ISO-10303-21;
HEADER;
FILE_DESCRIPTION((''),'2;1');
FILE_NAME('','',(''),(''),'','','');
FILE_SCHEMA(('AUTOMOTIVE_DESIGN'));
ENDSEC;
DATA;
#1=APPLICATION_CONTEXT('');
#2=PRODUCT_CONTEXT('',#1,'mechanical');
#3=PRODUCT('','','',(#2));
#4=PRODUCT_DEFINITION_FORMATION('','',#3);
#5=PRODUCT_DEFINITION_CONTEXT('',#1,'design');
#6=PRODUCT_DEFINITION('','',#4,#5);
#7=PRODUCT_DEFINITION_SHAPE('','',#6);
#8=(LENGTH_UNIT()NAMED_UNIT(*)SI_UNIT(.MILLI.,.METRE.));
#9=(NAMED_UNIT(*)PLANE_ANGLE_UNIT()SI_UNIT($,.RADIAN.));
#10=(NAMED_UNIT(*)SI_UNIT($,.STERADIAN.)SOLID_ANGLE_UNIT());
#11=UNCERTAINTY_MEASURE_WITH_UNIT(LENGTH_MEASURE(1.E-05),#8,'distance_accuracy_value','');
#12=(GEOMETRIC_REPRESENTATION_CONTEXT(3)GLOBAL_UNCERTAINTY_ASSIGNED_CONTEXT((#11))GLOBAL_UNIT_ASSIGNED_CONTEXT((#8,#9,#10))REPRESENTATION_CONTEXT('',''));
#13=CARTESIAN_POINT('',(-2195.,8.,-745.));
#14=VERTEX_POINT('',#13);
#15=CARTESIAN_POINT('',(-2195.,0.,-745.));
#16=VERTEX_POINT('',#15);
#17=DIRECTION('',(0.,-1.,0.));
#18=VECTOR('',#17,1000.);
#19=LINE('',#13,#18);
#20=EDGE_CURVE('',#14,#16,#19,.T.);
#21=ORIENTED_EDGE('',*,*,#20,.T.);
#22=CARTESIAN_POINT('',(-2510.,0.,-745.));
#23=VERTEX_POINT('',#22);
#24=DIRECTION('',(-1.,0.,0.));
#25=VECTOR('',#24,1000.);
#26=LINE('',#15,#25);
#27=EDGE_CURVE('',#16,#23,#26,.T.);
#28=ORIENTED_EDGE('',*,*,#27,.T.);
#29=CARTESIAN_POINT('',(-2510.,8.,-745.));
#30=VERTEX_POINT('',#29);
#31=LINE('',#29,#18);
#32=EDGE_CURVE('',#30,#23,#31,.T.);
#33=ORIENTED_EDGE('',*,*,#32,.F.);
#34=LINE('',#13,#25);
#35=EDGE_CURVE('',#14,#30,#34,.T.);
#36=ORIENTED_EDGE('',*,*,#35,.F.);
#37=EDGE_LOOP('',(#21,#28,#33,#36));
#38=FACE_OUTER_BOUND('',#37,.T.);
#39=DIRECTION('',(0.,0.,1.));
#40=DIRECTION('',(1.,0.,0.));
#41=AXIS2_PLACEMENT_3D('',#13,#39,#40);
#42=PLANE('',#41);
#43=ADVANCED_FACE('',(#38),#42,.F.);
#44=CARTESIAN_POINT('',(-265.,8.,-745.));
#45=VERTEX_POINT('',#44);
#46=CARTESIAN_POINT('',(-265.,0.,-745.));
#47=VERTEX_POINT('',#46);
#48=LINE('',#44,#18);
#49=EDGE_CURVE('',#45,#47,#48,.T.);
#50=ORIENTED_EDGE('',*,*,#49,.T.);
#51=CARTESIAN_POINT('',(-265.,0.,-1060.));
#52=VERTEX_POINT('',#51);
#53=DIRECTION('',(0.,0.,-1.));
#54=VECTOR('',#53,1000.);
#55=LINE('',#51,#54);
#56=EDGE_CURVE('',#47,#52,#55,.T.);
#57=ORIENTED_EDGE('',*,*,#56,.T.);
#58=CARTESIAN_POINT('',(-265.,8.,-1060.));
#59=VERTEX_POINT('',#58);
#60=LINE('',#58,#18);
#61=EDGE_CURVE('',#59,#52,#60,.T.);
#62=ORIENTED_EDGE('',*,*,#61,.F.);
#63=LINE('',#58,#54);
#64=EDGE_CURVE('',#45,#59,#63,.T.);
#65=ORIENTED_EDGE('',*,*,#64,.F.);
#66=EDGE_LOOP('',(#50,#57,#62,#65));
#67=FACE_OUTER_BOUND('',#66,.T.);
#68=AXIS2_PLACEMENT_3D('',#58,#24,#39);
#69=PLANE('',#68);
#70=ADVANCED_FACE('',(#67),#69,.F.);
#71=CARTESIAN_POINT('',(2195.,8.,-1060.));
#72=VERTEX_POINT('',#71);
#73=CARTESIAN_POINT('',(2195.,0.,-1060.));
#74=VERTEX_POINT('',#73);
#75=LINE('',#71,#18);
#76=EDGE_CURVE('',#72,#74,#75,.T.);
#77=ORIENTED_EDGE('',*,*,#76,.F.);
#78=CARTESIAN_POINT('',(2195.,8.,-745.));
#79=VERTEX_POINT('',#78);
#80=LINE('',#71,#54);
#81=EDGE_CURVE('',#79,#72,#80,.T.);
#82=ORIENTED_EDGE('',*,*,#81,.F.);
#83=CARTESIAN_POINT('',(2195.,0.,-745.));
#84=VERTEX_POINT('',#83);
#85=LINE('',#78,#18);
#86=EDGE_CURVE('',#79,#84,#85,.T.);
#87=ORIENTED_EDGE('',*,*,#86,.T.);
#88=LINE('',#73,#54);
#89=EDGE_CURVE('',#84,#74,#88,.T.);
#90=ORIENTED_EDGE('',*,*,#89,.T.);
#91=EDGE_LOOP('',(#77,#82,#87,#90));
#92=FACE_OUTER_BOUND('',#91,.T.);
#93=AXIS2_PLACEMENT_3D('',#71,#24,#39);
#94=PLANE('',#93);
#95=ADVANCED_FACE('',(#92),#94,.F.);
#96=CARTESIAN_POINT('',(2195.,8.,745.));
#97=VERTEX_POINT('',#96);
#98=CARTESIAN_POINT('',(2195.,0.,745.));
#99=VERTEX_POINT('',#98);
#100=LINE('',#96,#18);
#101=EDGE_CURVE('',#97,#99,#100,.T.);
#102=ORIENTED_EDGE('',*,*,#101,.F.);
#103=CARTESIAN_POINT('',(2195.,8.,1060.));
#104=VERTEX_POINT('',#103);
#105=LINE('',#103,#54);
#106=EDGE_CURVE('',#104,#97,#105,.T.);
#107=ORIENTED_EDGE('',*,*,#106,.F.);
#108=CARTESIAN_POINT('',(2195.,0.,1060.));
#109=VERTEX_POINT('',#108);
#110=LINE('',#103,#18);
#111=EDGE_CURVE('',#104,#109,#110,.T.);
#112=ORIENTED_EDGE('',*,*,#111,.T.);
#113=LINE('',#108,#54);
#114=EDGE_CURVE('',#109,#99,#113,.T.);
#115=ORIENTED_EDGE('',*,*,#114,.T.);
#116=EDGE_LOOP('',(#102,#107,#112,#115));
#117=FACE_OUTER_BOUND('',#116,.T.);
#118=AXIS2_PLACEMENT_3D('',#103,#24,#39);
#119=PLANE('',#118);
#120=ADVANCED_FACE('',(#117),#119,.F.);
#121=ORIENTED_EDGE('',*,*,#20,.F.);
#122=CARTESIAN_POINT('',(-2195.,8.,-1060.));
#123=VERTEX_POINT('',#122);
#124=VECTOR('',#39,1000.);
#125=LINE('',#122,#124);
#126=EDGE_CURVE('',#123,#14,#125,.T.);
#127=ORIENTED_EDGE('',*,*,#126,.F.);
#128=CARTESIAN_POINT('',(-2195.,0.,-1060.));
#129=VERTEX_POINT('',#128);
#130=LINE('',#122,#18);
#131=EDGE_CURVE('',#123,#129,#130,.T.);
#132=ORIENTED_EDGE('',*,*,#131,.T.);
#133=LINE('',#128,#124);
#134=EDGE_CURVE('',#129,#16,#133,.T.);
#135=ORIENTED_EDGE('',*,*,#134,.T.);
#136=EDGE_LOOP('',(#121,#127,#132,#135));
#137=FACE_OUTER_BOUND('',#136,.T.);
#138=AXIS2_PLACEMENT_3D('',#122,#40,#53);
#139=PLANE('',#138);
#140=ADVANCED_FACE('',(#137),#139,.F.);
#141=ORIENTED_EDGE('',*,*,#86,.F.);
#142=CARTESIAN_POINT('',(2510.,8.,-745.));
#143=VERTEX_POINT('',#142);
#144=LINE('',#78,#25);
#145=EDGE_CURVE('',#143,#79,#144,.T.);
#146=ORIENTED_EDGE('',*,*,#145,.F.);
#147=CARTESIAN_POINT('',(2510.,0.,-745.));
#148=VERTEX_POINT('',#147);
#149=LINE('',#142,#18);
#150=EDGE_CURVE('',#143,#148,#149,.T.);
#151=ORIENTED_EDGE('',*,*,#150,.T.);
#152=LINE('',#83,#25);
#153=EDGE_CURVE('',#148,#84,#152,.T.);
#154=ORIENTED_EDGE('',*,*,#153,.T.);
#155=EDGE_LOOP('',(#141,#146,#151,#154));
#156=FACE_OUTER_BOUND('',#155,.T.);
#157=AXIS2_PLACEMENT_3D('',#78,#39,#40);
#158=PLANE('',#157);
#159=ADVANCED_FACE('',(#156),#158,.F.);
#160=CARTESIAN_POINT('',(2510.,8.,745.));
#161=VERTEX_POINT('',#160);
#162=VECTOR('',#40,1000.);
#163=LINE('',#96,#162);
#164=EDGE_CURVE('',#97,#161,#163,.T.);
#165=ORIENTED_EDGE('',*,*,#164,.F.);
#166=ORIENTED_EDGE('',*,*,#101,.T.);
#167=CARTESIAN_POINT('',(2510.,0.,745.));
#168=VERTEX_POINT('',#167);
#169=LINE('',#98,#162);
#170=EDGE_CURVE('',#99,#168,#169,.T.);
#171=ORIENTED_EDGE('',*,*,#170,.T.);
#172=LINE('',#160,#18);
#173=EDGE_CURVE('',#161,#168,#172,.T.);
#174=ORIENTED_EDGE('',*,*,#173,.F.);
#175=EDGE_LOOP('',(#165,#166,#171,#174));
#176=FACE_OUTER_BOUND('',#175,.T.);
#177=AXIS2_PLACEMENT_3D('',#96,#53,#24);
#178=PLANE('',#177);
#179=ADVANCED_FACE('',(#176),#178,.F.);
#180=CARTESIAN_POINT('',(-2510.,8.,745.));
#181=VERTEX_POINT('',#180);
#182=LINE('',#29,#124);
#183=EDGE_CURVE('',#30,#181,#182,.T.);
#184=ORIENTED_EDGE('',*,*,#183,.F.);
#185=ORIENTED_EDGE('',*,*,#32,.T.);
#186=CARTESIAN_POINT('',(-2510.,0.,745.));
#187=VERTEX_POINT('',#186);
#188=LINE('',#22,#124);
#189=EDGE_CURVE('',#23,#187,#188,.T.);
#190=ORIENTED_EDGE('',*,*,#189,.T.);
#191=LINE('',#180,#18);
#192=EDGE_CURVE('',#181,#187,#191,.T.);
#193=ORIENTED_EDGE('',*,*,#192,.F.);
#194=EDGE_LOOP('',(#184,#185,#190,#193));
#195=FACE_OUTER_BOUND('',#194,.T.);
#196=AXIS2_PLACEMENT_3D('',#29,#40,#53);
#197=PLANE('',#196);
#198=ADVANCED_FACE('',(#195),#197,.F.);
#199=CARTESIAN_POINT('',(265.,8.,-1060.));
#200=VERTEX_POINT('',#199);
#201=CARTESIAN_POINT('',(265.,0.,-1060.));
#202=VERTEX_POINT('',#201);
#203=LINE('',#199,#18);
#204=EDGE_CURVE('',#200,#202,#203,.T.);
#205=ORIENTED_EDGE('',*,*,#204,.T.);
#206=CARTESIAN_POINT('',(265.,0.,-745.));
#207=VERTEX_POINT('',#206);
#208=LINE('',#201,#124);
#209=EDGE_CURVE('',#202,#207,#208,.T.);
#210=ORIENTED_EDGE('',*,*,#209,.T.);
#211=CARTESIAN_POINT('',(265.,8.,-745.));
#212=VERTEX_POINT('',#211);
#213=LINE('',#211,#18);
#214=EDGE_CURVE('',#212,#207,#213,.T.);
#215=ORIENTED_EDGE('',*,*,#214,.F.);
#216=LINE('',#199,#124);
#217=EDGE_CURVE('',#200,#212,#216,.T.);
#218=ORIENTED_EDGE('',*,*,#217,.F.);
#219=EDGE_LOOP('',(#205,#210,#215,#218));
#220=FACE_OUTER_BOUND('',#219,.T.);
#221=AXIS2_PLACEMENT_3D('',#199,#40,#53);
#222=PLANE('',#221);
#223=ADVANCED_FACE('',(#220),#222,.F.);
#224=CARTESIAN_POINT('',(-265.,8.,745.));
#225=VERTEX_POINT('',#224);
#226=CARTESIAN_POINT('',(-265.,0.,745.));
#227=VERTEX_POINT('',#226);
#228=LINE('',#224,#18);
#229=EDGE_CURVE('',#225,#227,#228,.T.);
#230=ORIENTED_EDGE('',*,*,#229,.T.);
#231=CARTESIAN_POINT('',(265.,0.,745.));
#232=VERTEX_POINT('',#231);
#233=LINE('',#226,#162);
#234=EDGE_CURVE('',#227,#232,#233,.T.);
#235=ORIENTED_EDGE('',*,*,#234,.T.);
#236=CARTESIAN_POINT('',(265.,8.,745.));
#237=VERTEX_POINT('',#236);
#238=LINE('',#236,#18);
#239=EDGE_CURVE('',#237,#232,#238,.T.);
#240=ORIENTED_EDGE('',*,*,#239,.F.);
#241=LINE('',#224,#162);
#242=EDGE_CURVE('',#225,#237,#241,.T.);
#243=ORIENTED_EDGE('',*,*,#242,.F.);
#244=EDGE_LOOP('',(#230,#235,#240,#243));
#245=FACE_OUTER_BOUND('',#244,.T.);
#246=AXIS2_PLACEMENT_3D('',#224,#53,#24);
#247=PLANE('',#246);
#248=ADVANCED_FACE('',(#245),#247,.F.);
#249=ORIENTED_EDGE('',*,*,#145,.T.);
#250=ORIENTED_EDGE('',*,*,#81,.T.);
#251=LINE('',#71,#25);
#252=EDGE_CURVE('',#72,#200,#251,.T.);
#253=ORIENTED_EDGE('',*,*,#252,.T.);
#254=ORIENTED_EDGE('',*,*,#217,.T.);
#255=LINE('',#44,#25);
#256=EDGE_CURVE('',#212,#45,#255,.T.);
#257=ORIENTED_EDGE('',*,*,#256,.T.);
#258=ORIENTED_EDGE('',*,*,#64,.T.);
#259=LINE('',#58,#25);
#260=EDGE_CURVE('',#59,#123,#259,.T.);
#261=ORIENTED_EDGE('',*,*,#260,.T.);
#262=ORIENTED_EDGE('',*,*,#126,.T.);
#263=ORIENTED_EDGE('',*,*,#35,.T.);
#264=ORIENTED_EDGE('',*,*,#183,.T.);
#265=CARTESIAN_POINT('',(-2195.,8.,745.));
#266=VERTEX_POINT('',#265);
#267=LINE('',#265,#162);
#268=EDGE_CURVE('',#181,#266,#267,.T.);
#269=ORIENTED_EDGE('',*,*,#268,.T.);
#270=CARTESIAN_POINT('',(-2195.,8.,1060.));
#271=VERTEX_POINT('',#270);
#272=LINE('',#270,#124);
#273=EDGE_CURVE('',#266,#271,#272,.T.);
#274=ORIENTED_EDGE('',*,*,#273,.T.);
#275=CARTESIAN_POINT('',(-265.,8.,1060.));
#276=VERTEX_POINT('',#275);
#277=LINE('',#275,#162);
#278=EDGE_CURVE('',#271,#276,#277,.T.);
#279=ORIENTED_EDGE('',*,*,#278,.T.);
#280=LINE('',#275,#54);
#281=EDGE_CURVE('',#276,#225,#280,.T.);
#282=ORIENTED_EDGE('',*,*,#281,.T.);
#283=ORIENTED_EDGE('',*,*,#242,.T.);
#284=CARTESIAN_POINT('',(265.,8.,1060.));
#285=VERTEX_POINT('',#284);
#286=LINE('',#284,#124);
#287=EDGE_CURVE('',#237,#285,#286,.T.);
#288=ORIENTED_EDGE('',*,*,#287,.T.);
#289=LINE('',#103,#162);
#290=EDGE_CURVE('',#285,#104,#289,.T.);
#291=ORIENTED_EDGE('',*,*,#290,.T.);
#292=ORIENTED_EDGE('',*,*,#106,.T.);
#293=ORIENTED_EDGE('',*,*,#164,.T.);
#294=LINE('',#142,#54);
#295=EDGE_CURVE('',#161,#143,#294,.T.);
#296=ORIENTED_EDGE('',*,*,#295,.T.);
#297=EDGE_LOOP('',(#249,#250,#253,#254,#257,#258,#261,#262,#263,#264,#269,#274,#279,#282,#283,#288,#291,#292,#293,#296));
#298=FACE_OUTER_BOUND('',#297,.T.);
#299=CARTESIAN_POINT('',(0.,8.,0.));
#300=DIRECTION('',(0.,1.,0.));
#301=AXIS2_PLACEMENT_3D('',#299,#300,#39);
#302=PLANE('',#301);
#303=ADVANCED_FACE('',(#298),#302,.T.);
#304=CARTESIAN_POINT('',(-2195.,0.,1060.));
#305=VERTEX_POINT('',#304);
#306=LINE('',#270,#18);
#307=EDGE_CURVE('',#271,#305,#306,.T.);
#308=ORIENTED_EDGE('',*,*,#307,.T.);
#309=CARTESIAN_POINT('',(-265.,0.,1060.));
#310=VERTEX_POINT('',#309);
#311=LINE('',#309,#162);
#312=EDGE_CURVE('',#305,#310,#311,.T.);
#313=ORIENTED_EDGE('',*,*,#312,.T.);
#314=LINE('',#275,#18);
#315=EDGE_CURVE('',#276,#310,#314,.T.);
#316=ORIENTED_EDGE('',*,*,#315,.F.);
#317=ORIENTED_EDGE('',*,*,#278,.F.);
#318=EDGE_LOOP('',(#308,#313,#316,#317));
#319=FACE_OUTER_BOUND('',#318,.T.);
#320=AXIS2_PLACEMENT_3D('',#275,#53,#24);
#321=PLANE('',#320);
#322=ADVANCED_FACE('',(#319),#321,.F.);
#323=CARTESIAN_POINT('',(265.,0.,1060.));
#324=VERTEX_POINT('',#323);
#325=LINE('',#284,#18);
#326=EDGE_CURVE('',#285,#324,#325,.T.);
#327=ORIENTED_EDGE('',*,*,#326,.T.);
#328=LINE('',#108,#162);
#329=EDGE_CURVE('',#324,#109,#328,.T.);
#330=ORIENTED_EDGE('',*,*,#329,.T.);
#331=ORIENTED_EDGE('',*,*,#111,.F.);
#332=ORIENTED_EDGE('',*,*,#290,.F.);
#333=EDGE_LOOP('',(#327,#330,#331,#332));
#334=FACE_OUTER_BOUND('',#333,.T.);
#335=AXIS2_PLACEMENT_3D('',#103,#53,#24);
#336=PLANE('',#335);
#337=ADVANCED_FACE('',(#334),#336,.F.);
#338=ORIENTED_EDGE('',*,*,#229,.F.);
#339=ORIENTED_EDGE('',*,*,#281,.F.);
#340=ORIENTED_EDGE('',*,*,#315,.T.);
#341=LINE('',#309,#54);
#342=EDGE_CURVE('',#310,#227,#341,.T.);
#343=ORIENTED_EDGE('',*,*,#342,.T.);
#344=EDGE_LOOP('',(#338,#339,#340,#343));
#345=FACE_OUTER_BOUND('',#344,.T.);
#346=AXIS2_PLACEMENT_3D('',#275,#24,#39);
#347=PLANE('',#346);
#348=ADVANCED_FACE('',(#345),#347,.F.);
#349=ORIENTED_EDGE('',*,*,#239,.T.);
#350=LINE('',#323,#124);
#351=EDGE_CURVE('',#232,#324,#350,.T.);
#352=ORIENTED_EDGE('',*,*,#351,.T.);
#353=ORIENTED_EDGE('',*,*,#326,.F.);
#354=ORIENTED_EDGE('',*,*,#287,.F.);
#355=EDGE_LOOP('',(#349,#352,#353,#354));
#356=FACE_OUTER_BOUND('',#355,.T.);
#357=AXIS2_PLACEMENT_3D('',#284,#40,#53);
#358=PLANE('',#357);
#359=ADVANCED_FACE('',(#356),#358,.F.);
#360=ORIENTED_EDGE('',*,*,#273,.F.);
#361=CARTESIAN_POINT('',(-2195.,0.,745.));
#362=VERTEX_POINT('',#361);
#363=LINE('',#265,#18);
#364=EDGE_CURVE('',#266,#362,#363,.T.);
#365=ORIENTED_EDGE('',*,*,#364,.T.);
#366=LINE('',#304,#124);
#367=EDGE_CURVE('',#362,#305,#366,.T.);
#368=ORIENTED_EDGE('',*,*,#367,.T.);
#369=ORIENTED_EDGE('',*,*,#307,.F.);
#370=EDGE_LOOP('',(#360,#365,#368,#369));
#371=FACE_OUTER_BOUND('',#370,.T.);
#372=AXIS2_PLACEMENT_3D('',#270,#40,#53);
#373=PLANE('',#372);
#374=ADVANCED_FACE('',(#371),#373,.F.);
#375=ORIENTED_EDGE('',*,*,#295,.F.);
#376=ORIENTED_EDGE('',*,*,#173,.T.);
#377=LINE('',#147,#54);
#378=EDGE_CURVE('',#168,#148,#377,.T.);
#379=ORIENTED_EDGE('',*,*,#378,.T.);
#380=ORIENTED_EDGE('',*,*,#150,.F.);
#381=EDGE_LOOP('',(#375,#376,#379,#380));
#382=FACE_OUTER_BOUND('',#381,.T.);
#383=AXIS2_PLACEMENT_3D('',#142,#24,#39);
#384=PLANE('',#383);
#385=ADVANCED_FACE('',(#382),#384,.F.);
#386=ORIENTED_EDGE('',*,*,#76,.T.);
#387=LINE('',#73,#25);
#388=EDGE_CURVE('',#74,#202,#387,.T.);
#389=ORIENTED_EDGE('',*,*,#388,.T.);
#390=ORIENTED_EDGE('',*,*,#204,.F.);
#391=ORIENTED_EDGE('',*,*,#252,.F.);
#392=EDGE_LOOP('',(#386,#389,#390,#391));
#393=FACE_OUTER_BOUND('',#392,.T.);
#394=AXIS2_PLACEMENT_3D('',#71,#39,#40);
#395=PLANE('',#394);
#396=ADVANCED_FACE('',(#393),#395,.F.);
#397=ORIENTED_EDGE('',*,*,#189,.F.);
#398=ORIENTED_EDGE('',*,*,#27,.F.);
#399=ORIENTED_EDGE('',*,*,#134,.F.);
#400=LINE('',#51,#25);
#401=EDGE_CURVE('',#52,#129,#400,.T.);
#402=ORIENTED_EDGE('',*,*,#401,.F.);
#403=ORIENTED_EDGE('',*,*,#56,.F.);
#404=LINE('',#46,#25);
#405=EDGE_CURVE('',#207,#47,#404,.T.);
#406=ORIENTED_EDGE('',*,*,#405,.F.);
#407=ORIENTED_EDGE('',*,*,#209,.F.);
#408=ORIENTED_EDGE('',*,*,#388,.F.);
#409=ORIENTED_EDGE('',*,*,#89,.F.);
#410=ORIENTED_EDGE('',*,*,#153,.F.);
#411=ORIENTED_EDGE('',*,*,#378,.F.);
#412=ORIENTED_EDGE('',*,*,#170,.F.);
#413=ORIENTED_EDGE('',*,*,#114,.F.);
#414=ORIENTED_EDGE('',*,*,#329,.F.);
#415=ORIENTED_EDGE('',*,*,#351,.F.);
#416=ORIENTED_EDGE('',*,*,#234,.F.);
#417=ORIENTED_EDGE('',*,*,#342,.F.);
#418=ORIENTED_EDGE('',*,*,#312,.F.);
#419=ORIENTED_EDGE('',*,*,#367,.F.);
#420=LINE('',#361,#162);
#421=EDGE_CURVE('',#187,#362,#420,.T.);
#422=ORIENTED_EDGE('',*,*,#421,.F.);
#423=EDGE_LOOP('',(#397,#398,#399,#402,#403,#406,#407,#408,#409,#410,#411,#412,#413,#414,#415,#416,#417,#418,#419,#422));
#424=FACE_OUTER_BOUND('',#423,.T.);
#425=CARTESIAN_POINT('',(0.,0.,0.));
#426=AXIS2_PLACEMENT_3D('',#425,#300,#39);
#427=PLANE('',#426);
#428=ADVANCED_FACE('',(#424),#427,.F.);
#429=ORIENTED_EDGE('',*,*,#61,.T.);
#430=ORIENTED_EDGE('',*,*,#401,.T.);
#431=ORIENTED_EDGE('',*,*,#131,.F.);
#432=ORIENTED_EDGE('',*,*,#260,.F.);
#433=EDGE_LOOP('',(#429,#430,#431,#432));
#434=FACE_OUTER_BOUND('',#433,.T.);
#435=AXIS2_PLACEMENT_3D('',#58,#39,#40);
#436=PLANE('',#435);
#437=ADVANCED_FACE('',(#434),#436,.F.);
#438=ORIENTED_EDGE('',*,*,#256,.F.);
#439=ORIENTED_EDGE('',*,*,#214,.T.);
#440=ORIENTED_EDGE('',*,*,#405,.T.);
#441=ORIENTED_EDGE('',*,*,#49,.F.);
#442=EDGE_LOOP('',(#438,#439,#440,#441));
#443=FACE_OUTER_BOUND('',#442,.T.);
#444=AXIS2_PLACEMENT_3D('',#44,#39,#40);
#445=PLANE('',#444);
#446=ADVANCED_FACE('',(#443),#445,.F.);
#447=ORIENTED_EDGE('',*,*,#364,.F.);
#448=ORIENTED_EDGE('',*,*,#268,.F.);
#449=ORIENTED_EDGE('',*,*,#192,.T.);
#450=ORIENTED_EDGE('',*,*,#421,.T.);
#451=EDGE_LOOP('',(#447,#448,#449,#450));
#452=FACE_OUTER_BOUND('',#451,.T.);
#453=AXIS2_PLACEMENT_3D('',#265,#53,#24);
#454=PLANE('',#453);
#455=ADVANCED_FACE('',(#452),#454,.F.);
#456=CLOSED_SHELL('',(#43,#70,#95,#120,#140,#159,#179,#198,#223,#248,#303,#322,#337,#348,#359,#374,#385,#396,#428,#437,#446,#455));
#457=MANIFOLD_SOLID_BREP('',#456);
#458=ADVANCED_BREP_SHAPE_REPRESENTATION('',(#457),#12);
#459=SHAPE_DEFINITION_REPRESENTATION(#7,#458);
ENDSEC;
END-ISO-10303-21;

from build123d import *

# Parameters (mm, degrees)
BOSS_EXTRUDE_1_DEPTH = 8


with BuildPart() as part:
    # Sketch 1 → Boss-Extrude 1 (new body)
    with BuildSketch(Plane(origin=(0, 0, 0), x_dir=(1, 0, 0), z_dir=(0, 1, 0))):
        Polygon((2195, 1060), (265, 1060), (265, 745), (-265, 745), (-265, 1060), (-2195, 1060), (-2195, 745), (-2510, 745), (-2510, -745), (-2195, -745), (-2195, -1060), (-265, -1060), (-265, -745), (265, -745), (265, -1060), (2195, -1060), (2195, -745), (2510, -745), (2510, 745), (2195, 745), align=None)
    extrude(amount=BOSS_EXTRUDE_1_DEPTH)


solid = part.part
